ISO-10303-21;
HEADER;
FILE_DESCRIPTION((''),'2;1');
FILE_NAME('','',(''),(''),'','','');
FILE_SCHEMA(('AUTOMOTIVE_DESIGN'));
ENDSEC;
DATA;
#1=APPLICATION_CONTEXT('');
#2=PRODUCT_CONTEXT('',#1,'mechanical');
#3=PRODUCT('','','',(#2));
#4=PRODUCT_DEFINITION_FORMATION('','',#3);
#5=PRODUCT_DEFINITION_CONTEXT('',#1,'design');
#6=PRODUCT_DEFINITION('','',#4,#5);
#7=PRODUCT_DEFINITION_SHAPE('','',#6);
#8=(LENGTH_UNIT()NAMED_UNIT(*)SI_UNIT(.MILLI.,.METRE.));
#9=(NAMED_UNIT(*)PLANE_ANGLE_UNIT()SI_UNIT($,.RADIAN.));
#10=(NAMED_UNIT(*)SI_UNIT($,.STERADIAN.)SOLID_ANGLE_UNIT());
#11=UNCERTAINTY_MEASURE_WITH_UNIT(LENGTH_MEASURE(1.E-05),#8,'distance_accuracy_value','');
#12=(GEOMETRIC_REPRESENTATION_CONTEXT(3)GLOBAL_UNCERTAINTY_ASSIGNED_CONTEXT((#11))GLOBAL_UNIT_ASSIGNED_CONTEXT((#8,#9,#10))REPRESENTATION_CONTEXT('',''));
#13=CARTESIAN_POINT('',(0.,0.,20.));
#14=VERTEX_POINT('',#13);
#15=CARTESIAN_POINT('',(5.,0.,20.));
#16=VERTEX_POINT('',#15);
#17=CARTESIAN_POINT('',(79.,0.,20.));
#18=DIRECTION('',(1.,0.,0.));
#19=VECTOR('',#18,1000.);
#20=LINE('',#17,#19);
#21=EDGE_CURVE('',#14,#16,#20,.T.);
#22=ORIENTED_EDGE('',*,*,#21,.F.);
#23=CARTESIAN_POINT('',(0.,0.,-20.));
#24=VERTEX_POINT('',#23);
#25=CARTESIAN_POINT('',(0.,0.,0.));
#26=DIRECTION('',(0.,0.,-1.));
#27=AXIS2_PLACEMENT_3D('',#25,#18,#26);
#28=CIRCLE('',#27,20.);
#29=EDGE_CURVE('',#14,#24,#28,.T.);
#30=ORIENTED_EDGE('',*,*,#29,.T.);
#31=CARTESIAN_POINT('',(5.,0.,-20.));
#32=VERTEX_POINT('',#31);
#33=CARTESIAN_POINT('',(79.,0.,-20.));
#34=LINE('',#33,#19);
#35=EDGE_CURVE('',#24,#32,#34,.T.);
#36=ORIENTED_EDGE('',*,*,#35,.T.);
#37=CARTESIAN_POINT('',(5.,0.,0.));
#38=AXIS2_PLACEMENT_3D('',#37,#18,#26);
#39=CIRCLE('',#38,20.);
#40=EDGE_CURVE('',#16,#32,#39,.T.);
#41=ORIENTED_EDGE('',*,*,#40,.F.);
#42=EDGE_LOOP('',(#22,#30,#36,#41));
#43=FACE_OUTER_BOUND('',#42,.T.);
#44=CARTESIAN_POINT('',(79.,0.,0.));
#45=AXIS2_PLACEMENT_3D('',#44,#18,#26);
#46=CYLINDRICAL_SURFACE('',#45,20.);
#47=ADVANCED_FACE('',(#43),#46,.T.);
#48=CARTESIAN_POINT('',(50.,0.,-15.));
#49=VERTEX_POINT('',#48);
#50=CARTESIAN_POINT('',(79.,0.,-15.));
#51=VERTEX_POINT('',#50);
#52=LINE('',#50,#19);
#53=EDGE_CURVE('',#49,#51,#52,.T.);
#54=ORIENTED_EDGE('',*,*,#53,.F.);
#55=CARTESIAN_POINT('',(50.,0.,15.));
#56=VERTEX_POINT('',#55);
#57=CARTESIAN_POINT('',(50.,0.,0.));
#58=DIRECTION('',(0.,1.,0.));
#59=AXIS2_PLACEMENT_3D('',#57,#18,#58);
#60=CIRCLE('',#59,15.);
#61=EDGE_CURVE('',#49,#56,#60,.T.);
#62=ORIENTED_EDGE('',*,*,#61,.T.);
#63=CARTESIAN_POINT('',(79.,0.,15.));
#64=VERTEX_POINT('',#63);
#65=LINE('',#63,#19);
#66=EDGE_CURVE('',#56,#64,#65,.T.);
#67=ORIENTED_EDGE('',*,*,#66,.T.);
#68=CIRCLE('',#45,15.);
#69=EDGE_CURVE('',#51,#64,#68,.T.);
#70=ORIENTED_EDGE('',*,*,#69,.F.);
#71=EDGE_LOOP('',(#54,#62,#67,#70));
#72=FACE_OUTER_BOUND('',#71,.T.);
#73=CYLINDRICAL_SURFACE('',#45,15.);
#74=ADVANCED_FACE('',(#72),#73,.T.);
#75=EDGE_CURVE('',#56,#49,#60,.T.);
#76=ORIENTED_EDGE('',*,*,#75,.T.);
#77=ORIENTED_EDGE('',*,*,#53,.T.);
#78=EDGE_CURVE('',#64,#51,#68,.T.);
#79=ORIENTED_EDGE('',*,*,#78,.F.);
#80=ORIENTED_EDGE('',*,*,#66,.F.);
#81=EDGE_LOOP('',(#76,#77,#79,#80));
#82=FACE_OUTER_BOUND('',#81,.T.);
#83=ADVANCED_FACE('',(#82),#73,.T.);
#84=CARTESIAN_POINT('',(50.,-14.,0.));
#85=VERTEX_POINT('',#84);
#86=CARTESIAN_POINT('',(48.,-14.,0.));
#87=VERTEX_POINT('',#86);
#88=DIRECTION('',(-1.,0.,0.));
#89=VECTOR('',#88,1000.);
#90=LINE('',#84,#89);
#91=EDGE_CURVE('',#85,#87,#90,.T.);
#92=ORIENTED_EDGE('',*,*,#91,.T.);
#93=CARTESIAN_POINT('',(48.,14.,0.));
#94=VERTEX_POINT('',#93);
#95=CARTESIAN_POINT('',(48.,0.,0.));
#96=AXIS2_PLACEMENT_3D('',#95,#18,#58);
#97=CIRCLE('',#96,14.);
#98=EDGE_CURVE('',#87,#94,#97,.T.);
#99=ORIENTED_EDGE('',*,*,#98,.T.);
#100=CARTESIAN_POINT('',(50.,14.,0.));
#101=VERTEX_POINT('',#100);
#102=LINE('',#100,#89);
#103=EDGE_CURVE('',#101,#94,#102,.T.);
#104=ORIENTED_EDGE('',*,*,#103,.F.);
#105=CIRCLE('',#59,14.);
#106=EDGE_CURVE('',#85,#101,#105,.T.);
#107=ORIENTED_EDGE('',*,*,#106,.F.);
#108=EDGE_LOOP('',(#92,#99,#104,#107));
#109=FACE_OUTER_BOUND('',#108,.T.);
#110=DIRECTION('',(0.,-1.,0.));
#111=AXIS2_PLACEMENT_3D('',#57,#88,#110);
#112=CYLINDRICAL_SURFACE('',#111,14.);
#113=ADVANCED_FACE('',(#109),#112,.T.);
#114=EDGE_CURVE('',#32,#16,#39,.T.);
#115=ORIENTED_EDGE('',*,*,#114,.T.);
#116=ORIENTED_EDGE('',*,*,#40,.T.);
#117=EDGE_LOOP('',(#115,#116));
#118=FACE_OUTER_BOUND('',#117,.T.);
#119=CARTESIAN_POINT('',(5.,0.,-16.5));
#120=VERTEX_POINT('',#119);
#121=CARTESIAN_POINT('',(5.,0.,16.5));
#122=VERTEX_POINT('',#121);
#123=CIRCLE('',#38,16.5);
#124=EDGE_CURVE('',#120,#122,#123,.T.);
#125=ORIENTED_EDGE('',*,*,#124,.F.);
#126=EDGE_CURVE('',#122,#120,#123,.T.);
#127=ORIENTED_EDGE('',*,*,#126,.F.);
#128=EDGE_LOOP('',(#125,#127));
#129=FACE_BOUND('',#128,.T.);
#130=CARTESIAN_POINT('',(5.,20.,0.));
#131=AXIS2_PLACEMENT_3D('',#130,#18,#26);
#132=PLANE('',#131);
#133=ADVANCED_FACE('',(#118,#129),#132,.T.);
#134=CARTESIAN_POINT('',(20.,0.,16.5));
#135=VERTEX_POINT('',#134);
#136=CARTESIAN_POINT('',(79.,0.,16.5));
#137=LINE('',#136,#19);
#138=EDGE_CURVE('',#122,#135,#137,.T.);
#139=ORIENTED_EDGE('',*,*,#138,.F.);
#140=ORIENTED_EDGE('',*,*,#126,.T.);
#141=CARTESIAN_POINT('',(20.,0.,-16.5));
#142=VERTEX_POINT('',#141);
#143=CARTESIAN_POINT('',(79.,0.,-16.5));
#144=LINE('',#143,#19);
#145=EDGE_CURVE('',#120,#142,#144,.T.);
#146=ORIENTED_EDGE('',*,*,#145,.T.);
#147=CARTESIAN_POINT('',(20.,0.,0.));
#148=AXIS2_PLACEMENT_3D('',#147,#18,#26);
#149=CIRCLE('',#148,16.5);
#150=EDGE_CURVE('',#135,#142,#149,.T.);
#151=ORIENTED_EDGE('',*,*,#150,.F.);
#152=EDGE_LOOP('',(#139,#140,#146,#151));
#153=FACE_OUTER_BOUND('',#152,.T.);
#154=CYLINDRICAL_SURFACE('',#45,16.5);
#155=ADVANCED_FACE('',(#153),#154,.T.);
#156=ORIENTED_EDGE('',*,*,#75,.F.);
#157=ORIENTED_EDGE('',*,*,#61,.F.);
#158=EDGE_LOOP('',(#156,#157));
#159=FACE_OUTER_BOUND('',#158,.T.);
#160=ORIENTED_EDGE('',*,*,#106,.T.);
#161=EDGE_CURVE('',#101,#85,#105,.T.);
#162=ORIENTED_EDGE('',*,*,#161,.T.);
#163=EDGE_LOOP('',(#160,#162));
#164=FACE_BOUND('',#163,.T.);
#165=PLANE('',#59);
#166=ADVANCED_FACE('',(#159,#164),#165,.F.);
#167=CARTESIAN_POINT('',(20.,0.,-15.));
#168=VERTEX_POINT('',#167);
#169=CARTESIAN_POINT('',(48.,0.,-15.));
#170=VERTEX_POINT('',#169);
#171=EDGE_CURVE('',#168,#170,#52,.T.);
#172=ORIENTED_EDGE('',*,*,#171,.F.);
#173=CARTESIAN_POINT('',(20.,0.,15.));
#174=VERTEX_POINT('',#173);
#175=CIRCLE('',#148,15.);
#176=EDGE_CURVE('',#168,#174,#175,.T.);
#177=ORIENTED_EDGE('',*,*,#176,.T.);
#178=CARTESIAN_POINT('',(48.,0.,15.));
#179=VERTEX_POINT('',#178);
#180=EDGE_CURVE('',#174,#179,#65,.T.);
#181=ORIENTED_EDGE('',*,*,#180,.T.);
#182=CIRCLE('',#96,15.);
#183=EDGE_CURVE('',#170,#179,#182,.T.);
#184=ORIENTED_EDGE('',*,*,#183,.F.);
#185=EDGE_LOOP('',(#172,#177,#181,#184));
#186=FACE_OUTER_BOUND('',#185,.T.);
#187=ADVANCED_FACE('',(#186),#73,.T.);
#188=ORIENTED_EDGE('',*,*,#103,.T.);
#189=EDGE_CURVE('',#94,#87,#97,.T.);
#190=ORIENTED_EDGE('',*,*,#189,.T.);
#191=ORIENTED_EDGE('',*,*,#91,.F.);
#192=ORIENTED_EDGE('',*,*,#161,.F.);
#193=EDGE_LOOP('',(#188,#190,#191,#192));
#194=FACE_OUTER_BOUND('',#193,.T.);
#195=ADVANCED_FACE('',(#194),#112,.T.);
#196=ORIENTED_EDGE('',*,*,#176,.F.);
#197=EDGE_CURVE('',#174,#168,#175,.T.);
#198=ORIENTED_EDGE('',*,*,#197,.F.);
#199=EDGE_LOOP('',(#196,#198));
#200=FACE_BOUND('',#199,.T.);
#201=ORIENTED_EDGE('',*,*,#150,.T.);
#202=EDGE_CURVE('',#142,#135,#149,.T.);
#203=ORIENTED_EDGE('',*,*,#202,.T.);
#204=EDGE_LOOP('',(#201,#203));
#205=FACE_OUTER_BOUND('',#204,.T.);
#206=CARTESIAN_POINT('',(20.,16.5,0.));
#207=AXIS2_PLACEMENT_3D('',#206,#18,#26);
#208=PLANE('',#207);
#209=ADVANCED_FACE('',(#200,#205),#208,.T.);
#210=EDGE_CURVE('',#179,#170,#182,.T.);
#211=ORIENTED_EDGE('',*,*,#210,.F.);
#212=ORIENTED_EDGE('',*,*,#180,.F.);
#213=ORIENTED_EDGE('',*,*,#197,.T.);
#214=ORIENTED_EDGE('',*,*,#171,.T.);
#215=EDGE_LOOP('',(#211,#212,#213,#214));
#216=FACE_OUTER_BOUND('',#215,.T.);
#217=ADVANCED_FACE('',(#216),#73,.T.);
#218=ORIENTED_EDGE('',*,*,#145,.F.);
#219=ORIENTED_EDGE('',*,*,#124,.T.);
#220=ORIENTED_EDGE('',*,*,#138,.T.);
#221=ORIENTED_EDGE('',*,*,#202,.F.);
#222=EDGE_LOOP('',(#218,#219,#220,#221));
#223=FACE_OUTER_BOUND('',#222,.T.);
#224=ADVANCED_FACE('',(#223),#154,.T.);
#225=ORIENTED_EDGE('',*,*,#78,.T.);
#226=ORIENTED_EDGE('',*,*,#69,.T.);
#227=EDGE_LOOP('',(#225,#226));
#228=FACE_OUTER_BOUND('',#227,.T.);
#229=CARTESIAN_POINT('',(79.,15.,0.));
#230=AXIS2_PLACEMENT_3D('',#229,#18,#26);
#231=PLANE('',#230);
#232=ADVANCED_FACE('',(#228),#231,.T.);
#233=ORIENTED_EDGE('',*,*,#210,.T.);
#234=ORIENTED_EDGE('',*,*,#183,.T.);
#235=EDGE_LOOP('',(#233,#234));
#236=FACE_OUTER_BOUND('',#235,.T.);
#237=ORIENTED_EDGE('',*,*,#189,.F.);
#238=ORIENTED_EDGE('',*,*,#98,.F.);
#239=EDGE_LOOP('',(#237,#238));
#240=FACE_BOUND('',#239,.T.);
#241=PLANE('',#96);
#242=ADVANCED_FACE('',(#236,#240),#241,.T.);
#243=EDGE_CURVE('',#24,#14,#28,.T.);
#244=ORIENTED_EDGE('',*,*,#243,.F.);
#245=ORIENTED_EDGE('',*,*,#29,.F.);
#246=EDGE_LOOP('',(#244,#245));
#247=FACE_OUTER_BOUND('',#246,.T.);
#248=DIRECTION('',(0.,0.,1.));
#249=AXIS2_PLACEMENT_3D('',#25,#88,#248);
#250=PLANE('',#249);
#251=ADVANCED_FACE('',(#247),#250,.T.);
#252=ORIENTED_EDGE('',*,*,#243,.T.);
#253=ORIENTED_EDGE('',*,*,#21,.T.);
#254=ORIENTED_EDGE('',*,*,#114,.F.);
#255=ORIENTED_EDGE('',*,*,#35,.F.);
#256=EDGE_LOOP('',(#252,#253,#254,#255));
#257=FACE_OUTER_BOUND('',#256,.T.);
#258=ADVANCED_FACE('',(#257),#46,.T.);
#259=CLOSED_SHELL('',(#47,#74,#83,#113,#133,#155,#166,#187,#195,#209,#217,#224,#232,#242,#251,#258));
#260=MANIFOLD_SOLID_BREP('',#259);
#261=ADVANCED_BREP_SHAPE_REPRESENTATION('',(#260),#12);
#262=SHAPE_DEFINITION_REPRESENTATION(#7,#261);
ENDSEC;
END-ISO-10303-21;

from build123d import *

# Parameters (mm, degrees)
CUT_EXTRUDE_START   = -29
SKETCH_3_R          = 15
SKETCH_3_R_2        = 14
CUT_EXTRUDE_1_DEPTH = 2


with BuildPart() as part:
    # 草图1 → 旋转1 (revolve)
    with BuildSketch(Plane.XY, mode=Mode.PRIVATE) as revolve_1_sk:
        Polygon((0, 0), (0, 20), (5, 20), (5, 16.5), (20, 16.5), (20, 15), (79, 15), (79, 0), align=None)
    revolve(revolve_1_sk.sketch.rotate(Axis((79, 0, 0), (-1, 0, 0)), 90), axis=Axis((79, 0, 0), (-1, 0, 0)))

    # 草图3 → 切除-拉伸1 (cut)
    with BuildSketch(Plane(origin=(79, 0, 0), x_dir=(0, 0, -1), z_dir=(1, 0, 0)).offset(CUT_EXTRUDE_START)):
        Circle(SKETCH_3_R)
        with Locations(Location((0, 0, 0), (0, 0, 90))):
            Circle(SKETCH_3_R_2, mode=Mode.SUBTRACT)
    extrude(amount=-CUT_EXTRUDE_1_DEPTH, mode=Mode.SUBTRACT)


solid = part.part
